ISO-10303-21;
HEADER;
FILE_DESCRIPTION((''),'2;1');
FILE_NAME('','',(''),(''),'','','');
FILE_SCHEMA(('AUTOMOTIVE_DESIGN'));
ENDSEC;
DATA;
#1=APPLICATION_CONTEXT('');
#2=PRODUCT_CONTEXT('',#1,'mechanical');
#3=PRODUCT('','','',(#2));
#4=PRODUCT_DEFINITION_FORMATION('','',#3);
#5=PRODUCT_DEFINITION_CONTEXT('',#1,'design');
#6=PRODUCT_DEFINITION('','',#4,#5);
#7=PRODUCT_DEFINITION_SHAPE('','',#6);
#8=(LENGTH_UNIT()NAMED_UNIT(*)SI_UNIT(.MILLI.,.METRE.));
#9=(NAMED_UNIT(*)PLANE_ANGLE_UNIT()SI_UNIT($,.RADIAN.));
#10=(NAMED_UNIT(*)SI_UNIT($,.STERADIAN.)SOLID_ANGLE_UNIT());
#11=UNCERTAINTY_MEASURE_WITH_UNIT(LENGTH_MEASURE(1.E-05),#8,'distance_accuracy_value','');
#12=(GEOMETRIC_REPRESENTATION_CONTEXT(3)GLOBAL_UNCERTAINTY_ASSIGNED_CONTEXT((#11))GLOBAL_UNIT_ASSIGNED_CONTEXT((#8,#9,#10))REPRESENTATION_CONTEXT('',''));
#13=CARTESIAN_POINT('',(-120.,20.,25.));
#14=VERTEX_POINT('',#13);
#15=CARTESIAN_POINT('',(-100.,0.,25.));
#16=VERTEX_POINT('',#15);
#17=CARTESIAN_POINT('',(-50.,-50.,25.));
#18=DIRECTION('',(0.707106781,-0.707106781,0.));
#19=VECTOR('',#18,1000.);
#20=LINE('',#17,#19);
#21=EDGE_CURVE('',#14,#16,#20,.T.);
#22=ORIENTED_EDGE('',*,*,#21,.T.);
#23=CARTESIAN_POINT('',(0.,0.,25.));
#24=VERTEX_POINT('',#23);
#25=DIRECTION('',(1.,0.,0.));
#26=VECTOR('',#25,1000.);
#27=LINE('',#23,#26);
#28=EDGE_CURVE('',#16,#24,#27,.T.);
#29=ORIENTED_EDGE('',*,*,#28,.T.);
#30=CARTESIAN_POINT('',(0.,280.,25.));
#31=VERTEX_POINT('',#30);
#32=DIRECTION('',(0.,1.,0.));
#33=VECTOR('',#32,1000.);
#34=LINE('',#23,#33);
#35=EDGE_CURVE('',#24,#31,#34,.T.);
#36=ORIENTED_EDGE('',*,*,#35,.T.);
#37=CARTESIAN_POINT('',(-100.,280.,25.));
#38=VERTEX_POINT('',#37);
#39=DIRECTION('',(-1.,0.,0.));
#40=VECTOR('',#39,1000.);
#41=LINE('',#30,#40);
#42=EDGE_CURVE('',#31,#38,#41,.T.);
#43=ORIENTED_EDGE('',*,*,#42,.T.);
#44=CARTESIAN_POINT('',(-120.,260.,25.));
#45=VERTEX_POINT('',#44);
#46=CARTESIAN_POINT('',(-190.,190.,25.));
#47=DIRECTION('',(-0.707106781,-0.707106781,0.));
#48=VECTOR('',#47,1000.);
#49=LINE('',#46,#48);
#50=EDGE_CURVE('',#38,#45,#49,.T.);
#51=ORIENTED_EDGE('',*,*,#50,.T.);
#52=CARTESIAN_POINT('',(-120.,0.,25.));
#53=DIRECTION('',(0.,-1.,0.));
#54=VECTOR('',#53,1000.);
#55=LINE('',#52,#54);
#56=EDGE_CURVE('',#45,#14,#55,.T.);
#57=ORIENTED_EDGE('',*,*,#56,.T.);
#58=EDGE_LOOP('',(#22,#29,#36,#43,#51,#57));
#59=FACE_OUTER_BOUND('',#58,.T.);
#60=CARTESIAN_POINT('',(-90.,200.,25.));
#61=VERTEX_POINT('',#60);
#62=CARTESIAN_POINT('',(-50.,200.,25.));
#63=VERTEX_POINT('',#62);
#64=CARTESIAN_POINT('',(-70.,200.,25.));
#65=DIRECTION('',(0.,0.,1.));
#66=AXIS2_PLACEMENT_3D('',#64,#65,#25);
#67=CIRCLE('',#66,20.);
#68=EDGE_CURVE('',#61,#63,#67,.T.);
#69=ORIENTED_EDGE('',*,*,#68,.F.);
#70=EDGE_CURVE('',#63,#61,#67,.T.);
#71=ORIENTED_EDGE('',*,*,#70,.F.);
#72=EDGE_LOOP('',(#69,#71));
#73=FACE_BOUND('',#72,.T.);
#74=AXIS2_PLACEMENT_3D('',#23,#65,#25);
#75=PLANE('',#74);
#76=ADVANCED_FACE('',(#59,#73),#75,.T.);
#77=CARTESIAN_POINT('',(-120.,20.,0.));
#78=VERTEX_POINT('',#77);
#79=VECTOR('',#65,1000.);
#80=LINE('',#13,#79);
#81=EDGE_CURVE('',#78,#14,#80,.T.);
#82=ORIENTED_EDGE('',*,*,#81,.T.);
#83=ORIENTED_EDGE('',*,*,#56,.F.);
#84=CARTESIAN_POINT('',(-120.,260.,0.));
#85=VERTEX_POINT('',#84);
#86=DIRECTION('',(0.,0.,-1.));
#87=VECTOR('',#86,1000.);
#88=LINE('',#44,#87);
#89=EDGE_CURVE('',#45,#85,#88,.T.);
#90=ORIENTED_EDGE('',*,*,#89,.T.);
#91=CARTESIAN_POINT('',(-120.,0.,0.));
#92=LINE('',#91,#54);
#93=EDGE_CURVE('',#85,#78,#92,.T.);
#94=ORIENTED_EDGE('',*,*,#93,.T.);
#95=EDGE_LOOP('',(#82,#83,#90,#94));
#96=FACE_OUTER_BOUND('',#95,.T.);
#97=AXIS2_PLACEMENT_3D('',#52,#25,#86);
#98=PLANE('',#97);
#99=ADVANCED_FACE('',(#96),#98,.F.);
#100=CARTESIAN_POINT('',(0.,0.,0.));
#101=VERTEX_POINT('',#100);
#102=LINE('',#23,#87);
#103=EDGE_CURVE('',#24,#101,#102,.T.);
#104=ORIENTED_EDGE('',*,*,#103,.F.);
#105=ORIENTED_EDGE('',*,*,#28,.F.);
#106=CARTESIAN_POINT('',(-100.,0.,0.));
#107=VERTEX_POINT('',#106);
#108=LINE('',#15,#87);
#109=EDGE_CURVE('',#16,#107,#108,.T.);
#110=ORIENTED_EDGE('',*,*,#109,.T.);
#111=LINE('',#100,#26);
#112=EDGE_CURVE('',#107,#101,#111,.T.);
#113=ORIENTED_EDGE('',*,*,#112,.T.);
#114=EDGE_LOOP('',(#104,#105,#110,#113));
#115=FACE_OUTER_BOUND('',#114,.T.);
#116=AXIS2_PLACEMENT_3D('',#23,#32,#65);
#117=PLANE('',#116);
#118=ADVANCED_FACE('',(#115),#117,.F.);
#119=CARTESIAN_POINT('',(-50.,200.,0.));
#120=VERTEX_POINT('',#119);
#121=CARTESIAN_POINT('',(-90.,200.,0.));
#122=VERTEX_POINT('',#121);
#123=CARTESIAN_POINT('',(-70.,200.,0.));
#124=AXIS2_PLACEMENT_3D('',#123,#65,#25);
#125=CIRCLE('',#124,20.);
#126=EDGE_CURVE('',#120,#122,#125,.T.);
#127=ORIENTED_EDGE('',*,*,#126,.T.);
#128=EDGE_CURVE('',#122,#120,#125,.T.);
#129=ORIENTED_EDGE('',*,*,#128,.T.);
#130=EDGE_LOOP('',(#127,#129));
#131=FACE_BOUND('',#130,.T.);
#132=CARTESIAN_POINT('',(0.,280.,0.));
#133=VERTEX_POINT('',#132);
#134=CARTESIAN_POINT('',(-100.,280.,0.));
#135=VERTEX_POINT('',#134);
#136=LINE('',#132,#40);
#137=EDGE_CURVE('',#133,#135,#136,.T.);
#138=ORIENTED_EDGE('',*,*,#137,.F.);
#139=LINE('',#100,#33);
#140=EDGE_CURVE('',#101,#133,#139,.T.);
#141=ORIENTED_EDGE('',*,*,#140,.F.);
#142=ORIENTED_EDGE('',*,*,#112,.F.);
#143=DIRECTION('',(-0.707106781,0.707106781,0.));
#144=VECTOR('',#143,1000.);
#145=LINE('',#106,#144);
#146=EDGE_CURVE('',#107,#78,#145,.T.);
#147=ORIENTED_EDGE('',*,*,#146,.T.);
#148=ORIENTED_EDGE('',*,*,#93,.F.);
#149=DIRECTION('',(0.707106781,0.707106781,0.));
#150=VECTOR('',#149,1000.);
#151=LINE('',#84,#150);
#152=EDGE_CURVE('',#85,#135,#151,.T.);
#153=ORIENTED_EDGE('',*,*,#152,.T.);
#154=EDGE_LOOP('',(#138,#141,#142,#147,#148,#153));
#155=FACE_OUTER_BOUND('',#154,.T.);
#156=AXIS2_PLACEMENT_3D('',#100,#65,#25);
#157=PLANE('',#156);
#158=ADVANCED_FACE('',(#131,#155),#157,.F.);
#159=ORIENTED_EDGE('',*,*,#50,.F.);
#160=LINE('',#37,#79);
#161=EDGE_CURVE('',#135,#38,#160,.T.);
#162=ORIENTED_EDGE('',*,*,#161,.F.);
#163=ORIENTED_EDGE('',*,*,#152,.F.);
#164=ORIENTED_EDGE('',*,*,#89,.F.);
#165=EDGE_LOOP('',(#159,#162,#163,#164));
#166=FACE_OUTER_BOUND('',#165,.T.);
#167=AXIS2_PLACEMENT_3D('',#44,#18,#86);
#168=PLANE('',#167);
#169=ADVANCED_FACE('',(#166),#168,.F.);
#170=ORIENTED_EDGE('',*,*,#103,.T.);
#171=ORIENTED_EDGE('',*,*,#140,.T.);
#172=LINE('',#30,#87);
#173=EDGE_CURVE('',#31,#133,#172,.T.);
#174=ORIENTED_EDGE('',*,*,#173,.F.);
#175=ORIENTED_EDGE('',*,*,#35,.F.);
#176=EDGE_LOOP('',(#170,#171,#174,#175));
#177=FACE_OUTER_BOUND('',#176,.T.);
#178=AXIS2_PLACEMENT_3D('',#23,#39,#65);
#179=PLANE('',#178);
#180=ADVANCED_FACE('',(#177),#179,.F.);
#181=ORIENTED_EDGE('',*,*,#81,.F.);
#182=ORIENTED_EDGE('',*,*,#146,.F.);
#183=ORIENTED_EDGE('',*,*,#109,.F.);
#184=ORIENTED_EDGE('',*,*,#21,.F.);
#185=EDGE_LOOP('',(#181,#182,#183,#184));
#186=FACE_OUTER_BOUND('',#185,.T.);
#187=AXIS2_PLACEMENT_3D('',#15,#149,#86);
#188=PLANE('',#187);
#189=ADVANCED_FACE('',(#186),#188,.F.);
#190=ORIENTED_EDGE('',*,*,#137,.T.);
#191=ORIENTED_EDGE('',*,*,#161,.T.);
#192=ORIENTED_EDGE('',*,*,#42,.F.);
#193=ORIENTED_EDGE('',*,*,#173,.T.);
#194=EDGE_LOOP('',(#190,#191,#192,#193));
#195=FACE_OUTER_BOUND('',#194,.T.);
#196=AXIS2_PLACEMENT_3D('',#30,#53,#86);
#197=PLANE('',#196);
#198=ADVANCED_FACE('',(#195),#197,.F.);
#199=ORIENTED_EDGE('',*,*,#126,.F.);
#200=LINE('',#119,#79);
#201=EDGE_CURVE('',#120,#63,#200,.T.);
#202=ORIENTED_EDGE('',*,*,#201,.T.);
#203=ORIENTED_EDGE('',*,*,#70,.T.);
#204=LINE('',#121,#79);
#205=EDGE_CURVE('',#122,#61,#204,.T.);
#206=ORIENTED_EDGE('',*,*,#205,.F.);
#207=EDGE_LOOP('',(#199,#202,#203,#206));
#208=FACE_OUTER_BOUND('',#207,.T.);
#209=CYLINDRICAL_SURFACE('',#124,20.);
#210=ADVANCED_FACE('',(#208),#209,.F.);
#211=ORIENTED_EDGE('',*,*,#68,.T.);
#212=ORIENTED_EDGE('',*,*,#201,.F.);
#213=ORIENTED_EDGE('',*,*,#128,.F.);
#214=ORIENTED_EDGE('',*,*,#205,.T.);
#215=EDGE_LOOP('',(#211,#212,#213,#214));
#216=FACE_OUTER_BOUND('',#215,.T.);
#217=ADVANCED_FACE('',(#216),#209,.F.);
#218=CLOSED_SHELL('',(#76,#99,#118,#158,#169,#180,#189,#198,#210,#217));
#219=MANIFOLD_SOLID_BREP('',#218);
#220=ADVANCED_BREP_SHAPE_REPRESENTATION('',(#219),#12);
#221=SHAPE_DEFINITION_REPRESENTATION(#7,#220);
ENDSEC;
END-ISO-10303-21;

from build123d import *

# Parameters (mm, degrees)
SKETCH_1_W               = 120
SKETCH_1_H               = 280
EXTRUDE_1_DEPTH          = 25
CUT_EXTRUDE_1_DEPTH      = 306.655034312
CUT_EXTRUDE_1_DEPTH_BACK = 306.655034312
SKETCH_2_R               = 20
CHAMFER_1_SIZE           = 20


with BuildPart() as part:
    # 草图1 → 凸台-拉伸1 (new body)
    with BuildSketch(Plane.XY):
        with Locations((-60, 140)):
            Rectangle(SKETCH_1_W, SKETCH_1_H)
    extrude(amount=EXTRUDE_1_DEPTH)

    # 草图2 → 切除-拉伸1 (cut, two sides: drawn at the far end of the back side and taken through both)
    with BuildSketch(Plane.XY.offset(25).offset(-CUT_EXTRUDE_1_DEPTH_BACK)):
        with Locations((-70, 200)):
            Circle(SKETCH_2_R)
    extrude(amount=CUT_EXTRUDE_1_DEPTH + CUT_EXTRUDE_1_DEPTH_BACK, mode=Mode.SUBTRACT)

    # 倒角1
    chamfer_1_edges = [part.edges().sort_by_distance(p)[0] for p in [
        (-120, 0, 12.5),
        (-120, 280, 12.5),
    ]]
    chamfer(chamfer_1_edges, length=CHAMFER_1_SIZE)


solid = part.part
